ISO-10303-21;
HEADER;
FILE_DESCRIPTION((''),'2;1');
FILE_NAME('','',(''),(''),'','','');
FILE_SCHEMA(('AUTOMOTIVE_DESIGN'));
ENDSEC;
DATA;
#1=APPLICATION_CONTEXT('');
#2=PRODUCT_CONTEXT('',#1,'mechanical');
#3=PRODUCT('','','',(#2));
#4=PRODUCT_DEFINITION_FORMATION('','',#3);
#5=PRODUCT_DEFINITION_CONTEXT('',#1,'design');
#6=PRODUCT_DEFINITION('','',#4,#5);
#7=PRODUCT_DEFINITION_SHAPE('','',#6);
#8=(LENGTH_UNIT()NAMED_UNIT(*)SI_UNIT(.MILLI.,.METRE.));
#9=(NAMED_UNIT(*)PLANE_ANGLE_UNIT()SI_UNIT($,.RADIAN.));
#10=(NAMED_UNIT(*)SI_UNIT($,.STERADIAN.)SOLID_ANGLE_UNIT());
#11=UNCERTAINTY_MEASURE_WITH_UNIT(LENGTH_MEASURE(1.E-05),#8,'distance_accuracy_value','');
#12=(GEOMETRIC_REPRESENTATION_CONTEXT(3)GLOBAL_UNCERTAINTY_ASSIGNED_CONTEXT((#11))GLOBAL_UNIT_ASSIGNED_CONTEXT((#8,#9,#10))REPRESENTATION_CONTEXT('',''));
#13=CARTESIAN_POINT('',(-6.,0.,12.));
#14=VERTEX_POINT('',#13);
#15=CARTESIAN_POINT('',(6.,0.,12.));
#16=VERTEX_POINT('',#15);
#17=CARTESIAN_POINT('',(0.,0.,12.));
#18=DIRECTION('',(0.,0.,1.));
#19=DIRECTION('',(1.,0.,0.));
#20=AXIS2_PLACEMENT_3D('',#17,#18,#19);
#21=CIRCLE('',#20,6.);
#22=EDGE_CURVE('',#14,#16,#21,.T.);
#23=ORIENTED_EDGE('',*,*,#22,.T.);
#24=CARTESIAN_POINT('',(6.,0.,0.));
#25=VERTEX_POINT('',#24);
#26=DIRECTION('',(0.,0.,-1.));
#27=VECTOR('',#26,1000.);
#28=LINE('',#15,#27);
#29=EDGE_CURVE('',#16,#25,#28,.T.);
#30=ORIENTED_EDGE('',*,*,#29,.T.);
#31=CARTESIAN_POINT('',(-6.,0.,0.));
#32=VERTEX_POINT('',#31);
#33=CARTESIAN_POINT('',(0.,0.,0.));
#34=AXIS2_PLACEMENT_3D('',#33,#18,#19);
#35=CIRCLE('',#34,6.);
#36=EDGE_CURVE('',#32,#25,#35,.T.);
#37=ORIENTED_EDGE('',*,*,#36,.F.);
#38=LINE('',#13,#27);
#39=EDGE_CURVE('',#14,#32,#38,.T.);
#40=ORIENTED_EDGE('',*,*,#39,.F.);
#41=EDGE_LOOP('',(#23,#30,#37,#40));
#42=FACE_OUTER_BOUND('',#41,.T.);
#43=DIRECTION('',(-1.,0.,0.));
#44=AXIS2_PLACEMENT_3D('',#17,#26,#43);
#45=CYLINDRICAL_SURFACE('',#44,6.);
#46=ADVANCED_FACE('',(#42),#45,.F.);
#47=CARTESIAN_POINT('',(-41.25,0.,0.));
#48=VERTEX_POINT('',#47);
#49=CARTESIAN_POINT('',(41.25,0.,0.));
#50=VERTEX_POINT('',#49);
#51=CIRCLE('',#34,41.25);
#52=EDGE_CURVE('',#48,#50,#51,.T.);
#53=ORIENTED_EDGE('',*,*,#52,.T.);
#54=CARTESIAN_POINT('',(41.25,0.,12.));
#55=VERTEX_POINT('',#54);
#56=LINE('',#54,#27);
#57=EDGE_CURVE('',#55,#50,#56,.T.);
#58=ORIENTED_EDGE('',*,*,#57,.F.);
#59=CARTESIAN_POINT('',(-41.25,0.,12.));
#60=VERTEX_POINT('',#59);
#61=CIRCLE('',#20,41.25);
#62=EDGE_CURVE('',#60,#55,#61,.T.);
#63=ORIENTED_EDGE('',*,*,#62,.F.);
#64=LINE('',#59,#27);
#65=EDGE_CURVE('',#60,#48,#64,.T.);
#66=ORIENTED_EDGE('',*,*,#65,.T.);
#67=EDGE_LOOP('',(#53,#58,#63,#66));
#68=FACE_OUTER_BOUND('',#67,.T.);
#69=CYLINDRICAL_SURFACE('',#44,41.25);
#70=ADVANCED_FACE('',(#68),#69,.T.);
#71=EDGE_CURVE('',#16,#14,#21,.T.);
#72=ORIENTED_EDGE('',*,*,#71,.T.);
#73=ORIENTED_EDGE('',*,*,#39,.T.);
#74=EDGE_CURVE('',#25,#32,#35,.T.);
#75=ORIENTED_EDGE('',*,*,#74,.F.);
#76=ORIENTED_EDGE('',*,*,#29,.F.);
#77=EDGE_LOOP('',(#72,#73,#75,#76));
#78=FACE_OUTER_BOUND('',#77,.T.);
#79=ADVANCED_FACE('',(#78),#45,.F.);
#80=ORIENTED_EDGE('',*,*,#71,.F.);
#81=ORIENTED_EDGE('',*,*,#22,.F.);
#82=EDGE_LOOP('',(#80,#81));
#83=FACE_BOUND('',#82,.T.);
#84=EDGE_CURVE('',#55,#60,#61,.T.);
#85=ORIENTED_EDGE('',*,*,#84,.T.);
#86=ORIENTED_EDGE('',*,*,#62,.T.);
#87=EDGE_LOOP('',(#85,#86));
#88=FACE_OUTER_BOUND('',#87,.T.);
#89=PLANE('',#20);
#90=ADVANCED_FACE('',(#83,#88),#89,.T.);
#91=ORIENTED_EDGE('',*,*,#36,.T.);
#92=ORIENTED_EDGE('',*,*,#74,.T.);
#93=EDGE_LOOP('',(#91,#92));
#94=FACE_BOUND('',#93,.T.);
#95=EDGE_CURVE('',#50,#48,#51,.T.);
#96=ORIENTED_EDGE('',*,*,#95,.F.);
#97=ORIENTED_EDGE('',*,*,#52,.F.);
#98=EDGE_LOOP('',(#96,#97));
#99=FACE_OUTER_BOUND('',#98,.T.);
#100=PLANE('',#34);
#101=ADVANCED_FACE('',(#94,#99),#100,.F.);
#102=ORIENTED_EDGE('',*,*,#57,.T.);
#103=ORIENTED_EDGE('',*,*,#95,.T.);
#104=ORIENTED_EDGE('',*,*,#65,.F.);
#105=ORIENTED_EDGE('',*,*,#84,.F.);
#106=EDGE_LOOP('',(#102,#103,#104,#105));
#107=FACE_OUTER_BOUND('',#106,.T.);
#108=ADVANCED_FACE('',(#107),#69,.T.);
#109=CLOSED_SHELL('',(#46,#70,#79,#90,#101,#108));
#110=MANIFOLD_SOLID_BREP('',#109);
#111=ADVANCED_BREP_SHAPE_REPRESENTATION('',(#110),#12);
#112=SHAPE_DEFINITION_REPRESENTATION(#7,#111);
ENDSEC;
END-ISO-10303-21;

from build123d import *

# Parameters (mm, degrees)
SKETCH1_R           = 41.25
SKETCH1_R_2         = 6
BOSS_EXTRUDE1_DEPTH = 12


with BuildPart() as part:
    # Sketch1 → Boss-Extrude1 (new body)
    with BuildSketch(Plane.XY):
        Circle(SKETCH1_R)
        Circle(SKETCH1_R_2, mode=Mode.SUBTRACT)
    extrude(amount=BOSS_EXTRUDE1_DEPTH)


solid = part.part
